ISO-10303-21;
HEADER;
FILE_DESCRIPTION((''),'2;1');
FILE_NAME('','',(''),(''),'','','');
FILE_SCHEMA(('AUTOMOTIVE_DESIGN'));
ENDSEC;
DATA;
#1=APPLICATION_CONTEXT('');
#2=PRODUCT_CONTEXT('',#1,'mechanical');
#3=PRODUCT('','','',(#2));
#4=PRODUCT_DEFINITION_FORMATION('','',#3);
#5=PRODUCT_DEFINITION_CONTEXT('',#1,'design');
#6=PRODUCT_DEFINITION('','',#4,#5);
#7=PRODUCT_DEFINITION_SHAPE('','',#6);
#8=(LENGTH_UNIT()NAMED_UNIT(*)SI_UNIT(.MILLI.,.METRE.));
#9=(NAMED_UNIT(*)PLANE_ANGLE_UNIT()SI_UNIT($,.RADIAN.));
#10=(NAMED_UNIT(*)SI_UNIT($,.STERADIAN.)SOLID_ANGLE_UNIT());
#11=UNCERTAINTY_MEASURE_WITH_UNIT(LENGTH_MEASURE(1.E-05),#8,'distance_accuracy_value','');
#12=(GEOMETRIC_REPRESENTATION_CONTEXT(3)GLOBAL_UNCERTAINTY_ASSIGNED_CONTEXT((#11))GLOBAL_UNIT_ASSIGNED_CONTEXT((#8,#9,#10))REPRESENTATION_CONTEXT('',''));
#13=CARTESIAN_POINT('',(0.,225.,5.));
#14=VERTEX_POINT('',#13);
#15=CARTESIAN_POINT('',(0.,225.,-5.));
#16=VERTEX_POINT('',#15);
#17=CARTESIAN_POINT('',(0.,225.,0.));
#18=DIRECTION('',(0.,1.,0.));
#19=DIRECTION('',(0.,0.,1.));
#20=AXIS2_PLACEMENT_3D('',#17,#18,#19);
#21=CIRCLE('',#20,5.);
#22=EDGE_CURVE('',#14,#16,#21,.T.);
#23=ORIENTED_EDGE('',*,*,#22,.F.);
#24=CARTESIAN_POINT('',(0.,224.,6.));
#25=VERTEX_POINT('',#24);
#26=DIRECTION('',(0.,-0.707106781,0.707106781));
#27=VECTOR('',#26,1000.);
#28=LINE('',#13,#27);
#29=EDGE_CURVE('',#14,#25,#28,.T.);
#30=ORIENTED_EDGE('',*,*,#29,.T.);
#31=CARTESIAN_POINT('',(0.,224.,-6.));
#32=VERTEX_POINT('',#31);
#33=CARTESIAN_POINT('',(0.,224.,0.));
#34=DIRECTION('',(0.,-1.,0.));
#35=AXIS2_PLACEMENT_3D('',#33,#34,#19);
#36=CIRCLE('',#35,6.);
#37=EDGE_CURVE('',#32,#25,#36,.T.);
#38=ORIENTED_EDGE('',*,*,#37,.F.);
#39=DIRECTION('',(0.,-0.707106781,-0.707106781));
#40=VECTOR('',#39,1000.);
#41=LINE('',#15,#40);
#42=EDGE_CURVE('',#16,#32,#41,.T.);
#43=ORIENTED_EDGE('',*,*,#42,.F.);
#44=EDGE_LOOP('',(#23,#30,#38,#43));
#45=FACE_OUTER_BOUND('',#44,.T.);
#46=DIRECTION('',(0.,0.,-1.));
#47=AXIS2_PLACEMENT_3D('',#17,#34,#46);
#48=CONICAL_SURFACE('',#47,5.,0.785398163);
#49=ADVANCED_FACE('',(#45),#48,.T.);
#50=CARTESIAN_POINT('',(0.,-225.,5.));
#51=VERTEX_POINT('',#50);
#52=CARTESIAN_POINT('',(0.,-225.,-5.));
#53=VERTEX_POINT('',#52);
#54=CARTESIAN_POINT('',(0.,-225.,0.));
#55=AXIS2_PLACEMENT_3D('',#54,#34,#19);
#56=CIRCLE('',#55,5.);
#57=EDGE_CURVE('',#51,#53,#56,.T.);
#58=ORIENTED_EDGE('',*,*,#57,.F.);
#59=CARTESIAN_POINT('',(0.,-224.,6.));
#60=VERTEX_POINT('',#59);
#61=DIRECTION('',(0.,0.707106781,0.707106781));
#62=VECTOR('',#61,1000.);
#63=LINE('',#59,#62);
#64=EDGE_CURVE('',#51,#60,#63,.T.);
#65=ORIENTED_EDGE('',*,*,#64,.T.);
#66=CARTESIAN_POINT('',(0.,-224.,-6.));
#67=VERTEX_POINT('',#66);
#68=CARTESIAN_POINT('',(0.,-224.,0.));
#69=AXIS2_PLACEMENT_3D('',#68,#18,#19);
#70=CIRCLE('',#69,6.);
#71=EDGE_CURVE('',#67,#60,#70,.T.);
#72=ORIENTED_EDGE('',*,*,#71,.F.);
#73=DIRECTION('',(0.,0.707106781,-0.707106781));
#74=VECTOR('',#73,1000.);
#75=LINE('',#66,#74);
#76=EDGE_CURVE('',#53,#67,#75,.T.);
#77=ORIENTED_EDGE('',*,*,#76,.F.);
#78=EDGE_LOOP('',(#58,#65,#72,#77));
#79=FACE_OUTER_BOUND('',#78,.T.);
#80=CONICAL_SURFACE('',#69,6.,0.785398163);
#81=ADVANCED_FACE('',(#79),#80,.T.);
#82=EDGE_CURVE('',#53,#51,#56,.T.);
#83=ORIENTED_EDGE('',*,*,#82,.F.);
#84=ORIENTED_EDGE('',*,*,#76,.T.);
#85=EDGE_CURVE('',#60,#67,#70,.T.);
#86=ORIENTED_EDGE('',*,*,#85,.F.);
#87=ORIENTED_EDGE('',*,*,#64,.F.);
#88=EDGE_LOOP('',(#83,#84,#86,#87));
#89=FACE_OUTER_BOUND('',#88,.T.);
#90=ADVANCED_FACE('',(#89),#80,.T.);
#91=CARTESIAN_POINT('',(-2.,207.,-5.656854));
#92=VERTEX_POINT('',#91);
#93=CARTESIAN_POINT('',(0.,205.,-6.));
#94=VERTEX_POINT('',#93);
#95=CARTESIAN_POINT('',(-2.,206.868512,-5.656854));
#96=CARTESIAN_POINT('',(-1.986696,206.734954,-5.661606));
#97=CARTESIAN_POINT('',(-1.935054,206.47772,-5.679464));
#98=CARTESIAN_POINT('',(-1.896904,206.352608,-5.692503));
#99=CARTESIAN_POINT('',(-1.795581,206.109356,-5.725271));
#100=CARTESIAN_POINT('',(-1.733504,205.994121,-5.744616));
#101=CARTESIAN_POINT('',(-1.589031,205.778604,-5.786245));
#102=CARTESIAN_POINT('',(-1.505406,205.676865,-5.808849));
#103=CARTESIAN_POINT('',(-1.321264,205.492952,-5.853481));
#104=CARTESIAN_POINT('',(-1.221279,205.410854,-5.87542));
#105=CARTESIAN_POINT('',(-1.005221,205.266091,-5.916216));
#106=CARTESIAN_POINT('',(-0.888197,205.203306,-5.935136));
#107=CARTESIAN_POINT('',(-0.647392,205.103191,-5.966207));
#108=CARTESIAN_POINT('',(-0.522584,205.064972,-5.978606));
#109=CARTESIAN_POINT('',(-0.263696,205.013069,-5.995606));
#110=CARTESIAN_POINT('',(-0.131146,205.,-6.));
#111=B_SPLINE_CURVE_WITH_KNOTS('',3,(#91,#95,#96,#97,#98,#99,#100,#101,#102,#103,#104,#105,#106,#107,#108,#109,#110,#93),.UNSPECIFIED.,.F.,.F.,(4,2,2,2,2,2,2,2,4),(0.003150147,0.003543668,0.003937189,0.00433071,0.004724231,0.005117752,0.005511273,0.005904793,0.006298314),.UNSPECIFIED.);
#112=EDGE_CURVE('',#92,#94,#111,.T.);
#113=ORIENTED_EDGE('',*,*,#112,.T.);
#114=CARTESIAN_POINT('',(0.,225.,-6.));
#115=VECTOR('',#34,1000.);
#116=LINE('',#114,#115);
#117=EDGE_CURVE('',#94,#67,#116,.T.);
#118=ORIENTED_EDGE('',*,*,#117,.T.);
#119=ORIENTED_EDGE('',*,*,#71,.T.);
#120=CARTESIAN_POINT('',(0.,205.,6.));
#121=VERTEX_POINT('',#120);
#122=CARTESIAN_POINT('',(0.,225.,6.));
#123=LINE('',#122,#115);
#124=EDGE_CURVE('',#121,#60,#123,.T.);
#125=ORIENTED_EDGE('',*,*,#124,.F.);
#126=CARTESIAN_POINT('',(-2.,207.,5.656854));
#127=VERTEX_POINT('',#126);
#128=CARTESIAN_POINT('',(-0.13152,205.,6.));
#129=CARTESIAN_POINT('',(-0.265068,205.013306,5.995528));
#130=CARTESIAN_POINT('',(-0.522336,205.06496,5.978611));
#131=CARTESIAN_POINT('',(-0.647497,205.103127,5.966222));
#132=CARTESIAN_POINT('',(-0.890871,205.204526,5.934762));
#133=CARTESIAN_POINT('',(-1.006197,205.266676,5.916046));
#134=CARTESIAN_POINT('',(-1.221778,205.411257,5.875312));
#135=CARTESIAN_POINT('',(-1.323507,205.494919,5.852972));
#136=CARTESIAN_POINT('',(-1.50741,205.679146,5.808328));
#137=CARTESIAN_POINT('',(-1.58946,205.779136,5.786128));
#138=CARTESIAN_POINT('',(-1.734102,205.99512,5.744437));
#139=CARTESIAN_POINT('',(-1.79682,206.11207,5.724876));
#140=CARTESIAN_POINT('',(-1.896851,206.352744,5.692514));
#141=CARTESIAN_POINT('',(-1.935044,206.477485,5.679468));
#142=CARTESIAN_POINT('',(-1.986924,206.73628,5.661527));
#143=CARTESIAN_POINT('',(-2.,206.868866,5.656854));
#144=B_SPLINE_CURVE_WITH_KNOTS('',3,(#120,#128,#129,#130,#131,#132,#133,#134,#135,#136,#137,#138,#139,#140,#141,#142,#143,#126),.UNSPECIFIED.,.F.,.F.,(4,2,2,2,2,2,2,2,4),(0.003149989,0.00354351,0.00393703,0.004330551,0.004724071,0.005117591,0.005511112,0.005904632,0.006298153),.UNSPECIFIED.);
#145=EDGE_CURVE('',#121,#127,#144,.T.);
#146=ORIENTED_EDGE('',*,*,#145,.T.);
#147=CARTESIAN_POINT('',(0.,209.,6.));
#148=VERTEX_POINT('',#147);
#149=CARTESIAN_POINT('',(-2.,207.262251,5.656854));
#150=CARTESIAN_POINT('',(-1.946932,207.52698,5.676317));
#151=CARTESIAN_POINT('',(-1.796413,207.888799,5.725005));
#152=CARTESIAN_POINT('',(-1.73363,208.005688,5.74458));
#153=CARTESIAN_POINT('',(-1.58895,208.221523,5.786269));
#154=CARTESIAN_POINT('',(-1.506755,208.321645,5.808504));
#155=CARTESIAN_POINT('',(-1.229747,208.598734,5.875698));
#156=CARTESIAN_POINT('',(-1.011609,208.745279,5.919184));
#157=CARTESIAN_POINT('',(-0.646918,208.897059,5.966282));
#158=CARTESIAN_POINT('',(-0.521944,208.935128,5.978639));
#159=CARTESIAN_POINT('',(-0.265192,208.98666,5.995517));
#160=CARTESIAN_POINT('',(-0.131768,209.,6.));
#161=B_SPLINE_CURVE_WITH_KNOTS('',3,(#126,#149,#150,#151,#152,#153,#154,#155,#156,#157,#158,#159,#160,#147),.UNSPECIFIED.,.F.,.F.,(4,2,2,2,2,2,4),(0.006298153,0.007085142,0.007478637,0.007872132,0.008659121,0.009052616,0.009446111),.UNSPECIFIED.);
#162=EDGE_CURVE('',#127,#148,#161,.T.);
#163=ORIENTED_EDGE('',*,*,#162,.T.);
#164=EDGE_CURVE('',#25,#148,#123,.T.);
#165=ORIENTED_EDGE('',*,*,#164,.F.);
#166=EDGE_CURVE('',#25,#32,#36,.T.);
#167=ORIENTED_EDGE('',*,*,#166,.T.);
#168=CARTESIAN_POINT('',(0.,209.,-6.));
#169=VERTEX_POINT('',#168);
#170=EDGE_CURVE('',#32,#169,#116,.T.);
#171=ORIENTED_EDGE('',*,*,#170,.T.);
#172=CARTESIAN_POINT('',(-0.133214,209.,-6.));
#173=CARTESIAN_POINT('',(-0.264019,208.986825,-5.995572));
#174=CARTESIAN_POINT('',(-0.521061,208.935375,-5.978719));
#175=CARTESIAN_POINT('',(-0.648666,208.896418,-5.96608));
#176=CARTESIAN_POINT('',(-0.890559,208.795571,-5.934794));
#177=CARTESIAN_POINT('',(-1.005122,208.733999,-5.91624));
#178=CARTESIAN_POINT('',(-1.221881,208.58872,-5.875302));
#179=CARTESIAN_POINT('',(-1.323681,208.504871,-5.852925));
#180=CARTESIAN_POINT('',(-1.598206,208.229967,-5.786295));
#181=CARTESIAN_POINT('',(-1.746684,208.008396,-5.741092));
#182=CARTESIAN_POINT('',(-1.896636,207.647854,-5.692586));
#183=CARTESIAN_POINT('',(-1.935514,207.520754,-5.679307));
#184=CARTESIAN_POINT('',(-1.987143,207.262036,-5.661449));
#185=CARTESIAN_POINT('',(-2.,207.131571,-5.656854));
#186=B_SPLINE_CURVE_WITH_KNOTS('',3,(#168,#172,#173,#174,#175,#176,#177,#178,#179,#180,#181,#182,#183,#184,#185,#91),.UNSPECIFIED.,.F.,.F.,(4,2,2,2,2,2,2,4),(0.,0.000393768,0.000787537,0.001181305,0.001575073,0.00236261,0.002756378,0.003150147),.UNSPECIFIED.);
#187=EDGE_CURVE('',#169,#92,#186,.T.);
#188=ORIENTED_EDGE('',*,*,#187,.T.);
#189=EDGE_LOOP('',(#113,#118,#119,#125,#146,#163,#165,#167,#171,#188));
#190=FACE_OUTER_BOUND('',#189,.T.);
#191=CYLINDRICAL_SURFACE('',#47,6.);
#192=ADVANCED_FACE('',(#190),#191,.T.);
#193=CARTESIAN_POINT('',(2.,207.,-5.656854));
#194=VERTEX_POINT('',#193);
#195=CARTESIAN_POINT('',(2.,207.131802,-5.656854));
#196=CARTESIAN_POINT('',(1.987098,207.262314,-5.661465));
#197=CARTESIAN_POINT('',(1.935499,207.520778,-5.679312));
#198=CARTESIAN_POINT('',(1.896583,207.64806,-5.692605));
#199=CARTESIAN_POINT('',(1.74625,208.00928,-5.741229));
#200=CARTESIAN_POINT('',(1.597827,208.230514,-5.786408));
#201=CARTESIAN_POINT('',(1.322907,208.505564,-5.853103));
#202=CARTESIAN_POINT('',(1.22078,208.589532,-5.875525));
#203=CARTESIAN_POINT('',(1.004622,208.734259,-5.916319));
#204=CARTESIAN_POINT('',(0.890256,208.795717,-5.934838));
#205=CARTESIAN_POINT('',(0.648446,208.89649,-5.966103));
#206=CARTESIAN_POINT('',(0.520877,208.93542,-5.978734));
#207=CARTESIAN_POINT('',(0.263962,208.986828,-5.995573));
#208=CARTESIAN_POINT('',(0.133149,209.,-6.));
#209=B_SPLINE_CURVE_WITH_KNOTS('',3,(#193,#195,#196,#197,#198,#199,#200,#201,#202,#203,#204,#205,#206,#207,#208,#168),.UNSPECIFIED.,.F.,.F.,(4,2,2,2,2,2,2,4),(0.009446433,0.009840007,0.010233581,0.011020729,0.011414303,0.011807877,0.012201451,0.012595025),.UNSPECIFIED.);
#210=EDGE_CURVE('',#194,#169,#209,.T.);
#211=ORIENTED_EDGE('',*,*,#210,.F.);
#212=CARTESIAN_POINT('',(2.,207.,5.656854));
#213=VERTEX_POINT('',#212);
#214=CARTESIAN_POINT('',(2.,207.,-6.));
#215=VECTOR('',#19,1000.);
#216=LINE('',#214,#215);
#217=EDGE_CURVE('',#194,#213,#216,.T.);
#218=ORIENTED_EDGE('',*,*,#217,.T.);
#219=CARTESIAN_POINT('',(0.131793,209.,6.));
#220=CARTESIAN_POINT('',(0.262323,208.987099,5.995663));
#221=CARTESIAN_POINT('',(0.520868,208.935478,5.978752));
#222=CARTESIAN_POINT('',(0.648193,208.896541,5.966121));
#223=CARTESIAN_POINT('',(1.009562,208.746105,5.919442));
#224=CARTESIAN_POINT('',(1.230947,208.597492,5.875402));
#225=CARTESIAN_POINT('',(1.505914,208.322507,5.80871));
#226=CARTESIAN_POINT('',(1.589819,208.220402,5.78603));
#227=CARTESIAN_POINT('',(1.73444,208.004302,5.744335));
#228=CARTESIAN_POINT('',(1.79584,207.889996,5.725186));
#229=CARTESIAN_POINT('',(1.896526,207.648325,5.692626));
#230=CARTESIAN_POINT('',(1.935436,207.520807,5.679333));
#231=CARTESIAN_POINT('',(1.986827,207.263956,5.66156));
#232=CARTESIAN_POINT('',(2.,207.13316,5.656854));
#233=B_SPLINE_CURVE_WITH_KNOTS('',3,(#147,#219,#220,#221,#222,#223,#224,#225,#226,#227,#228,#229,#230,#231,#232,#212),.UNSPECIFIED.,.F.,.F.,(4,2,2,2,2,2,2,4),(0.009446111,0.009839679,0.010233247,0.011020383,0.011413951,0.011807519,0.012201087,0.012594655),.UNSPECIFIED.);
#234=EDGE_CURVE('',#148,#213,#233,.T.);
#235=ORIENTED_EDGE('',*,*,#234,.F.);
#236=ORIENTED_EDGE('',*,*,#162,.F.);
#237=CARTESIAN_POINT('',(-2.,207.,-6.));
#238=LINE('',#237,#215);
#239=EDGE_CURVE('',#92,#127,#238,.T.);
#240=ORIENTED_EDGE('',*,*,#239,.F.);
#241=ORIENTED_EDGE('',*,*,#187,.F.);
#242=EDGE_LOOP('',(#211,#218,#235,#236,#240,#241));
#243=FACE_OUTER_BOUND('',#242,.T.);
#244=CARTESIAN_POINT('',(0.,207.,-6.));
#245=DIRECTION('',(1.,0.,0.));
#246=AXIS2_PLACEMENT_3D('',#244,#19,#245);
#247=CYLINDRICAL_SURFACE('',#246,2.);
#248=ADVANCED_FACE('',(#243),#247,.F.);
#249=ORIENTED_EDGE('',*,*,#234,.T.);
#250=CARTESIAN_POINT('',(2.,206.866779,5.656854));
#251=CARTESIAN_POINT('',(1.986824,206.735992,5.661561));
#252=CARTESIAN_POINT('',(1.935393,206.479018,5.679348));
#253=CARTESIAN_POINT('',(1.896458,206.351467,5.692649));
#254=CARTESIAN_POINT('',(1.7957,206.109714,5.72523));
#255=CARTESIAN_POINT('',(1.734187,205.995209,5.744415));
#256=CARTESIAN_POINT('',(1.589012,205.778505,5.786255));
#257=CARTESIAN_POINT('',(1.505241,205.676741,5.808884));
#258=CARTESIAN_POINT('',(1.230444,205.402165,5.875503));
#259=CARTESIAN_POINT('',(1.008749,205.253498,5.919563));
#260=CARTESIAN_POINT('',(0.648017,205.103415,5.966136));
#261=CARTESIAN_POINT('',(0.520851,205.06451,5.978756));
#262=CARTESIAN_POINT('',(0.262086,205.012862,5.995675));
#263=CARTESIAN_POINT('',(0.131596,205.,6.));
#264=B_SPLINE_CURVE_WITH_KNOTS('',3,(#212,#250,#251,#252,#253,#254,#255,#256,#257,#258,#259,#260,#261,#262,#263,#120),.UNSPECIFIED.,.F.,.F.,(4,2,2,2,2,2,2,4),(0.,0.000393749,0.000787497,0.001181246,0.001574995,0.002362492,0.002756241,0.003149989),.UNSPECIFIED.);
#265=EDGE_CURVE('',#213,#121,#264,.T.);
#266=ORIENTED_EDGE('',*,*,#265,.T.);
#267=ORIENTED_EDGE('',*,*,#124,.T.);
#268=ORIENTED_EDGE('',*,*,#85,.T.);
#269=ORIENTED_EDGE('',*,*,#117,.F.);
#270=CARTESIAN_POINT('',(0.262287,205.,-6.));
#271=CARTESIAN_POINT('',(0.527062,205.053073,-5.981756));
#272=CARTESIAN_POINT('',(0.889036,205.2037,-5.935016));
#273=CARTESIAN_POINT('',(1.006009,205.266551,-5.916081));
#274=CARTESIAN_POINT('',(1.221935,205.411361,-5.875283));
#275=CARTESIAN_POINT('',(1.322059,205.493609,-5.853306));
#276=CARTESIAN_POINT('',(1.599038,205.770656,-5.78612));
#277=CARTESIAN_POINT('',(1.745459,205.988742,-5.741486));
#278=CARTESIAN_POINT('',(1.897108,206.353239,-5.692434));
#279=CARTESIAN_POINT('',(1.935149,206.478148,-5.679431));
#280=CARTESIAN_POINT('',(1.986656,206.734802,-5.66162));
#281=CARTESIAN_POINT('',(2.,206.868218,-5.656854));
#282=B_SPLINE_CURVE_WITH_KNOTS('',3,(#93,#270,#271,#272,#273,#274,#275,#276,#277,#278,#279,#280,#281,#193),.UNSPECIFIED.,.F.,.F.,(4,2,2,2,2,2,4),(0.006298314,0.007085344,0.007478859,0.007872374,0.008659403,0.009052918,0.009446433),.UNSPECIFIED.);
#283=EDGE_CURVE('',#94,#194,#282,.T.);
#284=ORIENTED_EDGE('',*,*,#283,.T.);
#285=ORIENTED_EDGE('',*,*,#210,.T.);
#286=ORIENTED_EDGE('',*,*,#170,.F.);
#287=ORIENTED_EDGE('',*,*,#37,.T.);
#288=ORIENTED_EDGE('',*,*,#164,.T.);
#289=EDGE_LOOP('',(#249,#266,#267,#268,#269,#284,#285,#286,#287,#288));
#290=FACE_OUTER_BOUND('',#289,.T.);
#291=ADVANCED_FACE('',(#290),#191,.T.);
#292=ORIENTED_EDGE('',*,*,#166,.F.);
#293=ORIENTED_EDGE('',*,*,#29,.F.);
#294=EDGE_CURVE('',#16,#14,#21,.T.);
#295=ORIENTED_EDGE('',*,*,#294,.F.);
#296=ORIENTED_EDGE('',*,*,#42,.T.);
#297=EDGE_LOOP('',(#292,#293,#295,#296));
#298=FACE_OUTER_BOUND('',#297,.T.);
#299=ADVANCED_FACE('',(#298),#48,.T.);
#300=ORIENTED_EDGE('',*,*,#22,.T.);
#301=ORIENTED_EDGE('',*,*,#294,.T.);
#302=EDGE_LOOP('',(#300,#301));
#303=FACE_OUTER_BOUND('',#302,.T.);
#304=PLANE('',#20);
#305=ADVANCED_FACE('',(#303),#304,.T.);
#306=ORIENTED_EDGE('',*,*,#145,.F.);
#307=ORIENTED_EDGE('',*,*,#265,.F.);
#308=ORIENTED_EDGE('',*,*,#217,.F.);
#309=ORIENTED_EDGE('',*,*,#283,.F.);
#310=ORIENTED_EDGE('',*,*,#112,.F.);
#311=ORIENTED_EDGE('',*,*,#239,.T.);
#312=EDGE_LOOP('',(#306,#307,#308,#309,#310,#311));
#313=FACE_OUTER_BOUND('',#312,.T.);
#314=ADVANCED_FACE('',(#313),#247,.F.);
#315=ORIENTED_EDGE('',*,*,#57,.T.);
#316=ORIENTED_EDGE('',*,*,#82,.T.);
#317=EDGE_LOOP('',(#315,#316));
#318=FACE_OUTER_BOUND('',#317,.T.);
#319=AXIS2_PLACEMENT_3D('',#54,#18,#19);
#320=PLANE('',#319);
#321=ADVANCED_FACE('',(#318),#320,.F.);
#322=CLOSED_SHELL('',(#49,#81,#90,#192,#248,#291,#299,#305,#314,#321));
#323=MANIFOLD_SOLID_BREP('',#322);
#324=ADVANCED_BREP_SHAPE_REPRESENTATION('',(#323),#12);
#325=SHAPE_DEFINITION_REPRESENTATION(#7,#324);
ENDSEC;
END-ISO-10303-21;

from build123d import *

# Parameters (mm, degrees)
SKETCH1_R               = 6
BOSS_EXTRUDE1_DEPTH     = 225
CHAMFER1_SIZE           = 1
CUT_EXTRUDE1_DEPTH      = 226.159943152
CUT_EXTRUDE1_DEPTH_BACK = 226.159943152
SKETCH2_R               = 2


with BuildPart() as part:
    # Sketch1 → Boss-Extrude1 (new, symmetric)
    with BuildSketch(Plane(origin=(0, 0, 0), x_dir=(1, 0, 0), z_dir=(0, 1, 0))):
        with Locations(Location((0, 0, 0), (0, 0, 270))):
            Circle(SKETCH1_R)
    extrude(amount=BOSS_EXTRUDE1_DEPTH, both=True)

    # Chamfer1
    chamfer1_edges = [part.edges().sort_by_distance(p)[0] for p in [
        (0, -225, -6),
        (0, 225, -6),
    ]]
    chamfer(chamfer1_edges, length=CHAMFER1_SIZE)

    # Sketch2 → Cut-Extrude1 (cut, two sides: drawn at the far end of the back side and taken through both)
    with BuildSketch(Plane.XY.offset(-CUT_EXTRUDE1_DEPTH_BACK)):
        with Locations(Location((0, 207, 0), (0, 0, 89.999999987))):
            Circle(SKETCH2_R)
    extrude(amount=CUT_EXTRUDE1_DEPTH + CUT_EXTRUDE1_DEPTH_BACK, mode=Mode.SUBTRACT)


solid = part.part
